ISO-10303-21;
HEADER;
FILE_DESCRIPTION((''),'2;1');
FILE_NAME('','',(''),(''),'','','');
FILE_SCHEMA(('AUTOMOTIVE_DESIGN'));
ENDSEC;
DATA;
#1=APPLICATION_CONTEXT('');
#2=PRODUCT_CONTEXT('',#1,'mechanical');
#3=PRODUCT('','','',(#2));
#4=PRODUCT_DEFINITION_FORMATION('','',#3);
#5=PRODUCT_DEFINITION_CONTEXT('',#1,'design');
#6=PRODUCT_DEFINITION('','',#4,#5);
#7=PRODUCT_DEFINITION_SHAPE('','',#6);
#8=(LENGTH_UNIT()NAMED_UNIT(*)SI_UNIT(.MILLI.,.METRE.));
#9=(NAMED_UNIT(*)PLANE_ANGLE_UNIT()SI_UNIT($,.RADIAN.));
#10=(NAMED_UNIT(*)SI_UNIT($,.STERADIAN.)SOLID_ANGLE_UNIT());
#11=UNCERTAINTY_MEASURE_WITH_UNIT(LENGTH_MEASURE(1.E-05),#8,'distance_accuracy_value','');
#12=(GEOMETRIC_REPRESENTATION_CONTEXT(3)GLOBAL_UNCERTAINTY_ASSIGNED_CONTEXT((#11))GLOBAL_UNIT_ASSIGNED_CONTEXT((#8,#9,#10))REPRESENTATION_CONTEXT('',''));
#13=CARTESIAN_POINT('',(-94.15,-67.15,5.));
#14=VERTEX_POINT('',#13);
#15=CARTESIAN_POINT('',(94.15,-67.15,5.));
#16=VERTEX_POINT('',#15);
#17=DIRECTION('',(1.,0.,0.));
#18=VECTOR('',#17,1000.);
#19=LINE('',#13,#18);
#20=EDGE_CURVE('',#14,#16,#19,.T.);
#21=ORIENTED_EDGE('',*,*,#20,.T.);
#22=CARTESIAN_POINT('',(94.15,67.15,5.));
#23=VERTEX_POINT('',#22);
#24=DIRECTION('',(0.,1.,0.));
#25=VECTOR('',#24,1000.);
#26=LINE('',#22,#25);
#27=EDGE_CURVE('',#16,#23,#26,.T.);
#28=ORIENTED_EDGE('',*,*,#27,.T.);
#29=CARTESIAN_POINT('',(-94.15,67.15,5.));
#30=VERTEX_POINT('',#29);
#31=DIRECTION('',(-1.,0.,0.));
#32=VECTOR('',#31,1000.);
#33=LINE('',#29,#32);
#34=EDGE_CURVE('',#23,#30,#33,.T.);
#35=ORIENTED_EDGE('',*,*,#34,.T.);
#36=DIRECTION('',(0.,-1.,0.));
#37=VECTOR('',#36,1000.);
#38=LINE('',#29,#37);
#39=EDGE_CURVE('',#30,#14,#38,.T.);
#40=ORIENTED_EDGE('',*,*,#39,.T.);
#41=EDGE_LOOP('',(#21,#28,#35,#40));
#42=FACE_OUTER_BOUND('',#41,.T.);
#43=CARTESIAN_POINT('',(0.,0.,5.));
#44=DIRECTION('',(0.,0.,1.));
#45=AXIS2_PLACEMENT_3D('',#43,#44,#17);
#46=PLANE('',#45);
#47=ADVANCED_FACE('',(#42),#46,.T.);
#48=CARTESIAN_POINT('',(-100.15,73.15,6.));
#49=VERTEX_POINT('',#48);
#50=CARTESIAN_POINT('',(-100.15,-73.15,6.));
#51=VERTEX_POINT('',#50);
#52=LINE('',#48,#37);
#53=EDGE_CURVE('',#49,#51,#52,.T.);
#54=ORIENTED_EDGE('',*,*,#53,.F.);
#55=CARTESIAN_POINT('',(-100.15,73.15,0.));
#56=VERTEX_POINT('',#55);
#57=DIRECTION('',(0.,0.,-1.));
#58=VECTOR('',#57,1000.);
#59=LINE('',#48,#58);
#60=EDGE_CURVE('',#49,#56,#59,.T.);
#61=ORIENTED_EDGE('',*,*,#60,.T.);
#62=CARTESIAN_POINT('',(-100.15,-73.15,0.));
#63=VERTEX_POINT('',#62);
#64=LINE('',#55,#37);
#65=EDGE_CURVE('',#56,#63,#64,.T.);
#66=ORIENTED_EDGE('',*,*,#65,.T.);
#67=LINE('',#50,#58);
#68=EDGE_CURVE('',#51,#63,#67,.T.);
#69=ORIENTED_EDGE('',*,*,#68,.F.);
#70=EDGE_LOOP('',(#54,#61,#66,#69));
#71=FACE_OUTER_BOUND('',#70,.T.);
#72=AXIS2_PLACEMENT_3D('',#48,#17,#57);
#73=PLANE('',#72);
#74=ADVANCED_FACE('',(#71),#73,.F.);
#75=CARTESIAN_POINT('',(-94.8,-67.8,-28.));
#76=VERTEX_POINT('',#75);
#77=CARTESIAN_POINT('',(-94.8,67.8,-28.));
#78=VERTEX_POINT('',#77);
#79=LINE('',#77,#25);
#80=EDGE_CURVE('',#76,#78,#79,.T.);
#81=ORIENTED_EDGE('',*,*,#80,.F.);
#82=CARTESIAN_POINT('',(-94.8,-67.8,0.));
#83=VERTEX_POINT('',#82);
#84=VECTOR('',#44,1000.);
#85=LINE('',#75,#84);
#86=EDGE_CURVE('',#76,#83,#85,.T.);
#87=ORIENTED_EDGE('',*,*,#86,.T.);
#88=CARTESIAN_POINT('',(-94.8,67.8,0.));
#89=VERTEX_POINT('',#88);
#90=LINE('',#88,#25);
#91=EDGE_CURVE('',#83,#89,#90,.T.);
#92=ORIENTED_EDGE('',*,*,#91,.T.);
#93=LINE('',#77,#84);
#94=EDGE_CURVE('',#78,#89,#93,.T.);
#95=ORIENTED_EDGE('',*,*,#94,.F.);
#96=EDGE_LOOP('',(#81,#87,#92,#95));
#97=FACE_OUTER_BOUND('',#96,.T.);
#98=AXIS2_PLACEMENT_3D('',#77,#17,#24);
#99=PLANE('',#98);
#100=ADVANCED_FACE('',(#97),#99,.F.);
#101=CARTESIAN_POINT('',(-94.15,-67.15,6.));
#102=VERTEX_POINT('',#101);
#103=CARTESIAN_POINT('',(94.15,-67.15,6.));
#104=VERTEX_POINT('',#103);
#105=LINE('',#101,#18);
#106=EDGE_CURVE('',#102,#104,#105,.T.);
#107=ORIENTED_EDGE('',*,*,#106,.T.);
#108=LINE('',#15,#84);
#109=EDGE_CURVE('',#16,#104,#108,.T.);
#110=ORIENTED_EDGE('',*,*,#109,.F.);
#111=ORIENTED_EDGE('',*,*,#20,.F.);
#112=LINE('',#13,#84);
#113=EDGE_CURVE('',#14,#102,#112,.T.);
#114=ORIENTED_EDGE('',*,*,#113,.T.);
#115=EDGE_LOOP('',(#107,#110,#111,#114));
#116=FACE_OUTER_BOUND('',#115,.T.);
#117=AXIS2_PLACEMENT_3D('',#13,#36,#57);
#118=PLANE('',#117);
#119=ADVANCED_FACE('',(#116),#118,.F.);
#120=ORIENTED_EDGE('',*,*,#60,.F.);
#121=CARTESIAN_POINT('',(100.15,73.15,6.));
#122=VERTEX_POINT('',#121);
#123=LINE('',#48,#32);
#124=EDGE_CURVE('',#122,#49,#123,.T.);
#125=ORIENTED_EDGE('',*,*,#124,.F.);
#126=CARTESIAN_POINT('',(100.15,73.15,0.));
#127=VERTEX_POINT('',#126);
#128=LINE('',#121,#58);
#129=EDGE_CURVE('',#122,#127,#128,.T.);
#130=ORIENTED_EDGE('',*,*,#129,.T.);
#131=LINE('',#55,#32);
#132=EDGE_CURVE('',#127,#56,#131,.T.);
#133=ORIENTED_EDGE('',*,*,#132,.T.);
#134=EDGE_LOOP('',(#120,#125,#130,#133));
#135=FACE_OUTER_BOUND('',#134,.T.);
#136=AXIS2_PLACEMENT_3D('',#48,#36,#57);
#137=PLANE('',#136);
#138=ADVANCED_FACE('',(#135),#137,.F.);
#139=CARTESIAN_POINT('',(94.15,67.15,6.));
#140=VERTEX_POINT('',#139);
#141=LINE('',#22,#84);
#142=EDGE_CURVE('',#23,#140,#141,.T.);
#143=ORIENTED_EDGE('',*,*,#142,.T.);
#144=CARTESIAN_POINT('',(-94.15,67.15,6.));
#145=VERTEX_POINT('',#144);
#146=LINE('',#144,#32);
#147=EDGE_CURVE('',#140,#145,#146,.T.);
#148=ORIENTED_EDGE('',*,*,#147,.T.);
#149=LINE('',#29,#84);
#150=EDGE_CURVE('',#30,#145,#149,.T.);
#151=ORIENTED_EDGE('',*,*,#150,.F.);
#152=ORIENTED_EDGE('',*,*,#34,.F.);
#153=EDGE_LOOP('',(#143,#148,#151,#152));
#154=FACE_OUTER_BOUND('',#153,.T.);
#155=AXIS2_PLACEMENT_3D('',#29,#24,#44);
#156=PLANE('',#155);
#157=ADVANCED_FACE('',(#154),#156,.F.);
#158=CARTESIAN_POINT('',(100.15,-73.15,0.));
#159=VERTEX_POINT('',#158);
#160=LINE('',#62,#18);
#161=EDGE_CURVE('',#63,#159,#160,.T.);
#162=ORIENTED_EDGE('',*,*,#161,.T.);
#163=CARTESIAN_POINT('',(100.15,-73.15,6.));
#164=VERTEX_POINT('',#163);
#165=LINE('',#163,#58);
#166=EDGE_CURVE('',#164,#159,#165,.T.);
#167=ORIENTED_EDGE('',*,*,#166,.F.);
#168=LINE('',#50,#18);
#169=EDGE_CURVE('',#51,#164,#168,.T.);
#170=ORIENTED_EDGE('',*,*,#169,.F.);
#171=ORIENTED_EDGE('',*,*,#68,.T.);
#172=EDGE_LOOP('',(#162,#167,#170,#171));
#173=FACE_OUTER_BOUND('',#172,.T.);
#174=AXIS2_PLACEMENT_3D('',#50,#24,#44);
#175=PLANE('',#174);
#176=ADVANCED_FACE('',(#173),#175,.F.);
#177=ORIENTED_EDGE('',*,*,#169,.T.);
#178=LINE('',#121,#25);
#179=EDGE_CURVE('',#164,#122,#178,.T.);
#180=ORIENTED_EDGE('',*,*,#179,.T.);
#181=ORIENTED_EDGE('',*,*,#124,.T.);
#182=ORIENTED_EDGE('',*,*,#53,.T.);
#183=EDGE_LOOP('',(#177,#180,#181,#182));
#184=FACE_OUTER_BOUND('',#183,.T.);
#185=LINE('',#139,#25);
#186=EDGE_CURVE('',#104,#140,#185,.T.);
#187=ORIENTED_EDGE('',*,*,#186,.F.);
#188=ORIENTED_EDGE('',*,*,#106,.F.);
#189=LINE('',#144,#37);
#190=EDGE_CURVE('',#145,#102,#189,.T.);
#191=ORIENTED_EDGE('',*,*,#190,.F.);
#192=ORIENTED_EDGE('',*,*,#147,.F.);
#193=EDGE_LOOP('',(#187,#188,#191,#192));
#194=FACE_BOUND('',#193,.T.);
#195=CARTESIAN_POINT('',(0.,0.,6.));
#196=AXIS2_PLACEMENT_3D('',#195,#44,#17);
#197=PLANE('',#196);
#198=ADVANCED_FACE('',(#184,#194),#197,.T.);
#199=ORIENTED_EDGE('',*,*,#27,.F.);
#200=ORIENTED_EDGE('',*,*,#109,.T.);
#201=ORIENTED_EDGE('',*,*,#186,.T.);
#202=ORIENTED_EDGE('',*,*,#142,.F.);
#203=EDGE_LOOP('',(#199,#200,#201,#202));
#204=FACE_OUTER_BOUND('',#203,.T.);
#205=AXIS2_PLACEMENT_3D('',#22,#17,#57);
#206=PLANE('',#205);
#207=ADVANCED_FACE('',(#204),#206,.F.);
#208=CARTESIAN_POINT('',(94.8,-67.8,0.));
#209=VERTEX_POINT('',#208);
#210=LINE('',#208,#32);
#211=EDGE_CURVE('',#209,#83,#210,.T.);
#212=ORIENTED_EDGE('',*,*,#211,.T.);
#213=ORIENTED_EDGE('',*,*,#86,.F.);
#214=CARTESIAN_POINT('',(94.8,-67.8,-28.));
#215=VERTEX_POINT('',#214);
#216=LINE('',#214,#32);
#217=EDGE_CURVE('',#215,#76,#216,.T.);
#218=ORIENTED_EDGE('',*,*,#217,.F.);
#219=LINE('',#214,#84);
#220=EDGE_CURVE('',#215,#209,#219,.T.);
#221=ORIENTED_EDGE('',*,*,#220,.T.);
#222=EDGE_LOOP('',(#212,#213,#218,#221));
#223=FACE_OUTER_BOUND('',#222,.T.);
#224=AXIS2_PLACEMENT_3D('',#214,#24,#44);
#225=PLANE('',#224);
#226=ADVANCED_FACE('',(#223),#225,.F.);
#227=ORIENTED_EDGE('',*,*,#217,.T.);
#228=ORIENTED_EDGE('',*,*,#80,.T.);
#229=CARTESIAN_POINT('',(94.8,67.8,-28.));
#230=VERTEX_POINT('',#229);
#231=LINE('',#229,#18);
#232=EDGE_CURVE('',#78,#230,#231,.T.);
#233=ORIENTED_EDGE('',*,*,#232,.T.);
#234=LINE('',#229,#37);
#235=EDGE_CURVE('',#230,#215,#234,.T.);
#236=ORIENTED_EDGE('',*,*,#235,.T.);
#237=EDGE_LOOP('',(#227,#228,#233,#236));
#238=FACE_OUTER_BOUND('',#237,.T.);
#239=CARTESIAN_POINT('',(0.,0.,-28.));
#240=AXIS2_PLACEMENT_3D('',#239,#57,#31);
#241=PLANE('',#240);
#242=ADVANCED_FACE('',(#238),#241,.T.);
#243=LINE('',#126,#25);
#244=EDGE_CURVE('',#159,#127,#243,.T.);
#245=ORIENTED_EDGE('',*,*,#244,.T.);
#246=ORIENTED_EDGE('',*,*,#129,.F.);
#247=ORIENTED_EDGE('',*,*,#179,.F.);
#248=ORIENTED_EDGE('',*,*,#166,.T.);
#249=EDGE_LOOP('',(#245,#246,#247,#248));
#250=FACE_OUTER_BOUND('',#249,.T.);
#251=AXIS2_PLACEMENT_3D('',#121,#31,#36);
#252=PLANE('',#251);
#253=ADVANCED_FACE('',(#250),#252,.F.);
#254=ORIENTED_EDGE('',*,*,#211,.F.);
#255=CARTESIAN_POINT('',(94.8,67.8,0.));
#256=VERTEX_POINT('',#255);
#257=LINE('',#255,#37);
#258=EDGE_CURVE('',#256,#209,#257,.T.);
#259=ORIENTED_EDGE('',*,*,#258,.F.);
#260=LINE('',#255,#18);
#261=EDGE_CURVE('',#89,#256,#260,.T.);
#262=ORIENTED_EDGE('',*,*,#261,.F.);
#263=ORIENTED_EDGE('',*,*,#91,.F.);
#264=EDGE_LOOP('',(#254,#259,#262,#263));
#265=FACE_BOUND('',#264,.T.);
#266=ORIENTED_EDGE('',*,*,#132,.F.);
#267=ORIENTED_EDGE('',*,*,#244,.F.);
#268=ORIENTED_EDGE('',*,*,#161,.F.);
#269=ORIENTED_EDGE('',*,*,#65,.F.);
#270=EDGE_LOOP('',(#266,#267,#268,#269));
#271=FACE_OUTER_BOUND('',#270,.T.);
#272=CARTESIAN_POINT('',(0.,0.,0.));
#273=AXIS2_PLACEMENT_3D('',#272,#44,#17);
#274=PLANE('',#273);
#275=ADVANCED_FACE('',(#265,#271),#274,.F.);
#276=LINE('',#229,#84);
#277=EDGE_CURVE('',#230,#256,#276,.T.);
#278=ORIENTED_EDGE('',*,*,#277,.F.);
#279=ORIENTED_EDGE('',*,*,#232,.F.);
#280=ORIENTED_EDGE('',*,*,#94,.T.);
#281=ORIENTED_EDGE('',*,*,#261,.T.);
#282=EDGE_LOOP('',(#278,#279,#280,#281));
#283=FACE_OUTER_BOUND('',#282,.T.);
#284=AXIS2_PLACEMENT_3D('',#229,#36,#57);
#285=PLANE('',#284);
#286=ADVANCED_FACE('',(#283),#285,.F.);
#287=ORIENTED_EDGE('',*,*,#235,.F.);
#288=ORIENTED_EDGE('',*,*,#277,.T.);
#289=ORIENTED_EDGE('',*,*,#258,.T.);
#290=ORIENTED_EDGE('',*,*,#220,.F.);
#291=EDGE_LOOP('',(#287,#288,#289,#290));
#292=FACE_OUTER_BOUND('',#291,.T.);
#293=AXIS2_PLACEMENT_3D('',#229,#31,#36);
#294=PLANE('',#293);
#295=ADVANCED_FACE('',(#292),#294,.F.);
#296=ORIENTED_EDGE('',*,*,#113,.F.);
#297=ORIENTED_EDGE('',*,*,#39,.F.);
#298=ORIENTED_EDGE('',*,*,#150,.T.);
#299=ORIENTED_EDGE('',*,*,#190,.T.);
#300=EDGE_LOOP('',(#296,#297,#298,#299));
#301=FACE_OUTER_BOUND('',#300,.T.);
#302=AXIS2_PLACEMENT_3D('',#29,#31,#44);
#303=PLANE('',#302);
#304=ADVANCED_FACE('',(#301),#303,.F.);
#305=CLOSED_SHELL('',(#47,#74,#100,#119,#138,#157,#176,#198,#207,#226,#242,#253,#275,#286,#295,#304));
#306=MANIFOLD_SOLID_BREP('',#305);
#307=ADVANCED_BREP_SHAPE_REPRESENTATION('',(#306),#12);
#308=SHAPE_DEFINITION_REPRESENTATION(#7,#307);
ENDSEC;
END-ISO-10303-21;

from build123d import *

# Parameters (mm, degrees)
SKETCH_1_W          = 200.3
SKETCH_1_H          = 146.3
EXTRUDE_1_DEPTH     = 6
SKETCH_2_W          = 189.6
SKETCH_2_H          = 135.6
EXTRUDE_2_DEPTH     = 28
SKETCH_3_W          = 188.3
SKETCH_3_H          = 134.3
CUT_EXTRUDE_1_DEPTH = 1


with BuildPart() as part:
    # 草图1 → 凸台-拉伸1 (new body)
    with BuildSketch(Plane.XY):
        Rectangle(SKETCH_1_W, SKETCH_1_H)
    extrude(amount=EXTRUDE_1_DEPTH)

    # 草图2 → 凸台-拉伸2 (add)
    with BuildSketch(Plane(origin=(0, 0, 0), x_dir=(-1, 0, 0), z_dir=(0, 0, -1))):
        Rectangle(SKETCH_2_W, SKETCH_2_H)
    extrude(amount=EXTRUDE_2_DEPTH)

    # 草图3 → 切除-拉伸1 (cut)
    with BuildSketch(Plane.XY.offset(6)):
        Rectangle(SKETCH_3_W, SKETCH_3_H)
    extrude(amount=-CUT_EXTRUDE_1_DEPTH, mode=Mode.SUBTRACT)


solid = part.part
